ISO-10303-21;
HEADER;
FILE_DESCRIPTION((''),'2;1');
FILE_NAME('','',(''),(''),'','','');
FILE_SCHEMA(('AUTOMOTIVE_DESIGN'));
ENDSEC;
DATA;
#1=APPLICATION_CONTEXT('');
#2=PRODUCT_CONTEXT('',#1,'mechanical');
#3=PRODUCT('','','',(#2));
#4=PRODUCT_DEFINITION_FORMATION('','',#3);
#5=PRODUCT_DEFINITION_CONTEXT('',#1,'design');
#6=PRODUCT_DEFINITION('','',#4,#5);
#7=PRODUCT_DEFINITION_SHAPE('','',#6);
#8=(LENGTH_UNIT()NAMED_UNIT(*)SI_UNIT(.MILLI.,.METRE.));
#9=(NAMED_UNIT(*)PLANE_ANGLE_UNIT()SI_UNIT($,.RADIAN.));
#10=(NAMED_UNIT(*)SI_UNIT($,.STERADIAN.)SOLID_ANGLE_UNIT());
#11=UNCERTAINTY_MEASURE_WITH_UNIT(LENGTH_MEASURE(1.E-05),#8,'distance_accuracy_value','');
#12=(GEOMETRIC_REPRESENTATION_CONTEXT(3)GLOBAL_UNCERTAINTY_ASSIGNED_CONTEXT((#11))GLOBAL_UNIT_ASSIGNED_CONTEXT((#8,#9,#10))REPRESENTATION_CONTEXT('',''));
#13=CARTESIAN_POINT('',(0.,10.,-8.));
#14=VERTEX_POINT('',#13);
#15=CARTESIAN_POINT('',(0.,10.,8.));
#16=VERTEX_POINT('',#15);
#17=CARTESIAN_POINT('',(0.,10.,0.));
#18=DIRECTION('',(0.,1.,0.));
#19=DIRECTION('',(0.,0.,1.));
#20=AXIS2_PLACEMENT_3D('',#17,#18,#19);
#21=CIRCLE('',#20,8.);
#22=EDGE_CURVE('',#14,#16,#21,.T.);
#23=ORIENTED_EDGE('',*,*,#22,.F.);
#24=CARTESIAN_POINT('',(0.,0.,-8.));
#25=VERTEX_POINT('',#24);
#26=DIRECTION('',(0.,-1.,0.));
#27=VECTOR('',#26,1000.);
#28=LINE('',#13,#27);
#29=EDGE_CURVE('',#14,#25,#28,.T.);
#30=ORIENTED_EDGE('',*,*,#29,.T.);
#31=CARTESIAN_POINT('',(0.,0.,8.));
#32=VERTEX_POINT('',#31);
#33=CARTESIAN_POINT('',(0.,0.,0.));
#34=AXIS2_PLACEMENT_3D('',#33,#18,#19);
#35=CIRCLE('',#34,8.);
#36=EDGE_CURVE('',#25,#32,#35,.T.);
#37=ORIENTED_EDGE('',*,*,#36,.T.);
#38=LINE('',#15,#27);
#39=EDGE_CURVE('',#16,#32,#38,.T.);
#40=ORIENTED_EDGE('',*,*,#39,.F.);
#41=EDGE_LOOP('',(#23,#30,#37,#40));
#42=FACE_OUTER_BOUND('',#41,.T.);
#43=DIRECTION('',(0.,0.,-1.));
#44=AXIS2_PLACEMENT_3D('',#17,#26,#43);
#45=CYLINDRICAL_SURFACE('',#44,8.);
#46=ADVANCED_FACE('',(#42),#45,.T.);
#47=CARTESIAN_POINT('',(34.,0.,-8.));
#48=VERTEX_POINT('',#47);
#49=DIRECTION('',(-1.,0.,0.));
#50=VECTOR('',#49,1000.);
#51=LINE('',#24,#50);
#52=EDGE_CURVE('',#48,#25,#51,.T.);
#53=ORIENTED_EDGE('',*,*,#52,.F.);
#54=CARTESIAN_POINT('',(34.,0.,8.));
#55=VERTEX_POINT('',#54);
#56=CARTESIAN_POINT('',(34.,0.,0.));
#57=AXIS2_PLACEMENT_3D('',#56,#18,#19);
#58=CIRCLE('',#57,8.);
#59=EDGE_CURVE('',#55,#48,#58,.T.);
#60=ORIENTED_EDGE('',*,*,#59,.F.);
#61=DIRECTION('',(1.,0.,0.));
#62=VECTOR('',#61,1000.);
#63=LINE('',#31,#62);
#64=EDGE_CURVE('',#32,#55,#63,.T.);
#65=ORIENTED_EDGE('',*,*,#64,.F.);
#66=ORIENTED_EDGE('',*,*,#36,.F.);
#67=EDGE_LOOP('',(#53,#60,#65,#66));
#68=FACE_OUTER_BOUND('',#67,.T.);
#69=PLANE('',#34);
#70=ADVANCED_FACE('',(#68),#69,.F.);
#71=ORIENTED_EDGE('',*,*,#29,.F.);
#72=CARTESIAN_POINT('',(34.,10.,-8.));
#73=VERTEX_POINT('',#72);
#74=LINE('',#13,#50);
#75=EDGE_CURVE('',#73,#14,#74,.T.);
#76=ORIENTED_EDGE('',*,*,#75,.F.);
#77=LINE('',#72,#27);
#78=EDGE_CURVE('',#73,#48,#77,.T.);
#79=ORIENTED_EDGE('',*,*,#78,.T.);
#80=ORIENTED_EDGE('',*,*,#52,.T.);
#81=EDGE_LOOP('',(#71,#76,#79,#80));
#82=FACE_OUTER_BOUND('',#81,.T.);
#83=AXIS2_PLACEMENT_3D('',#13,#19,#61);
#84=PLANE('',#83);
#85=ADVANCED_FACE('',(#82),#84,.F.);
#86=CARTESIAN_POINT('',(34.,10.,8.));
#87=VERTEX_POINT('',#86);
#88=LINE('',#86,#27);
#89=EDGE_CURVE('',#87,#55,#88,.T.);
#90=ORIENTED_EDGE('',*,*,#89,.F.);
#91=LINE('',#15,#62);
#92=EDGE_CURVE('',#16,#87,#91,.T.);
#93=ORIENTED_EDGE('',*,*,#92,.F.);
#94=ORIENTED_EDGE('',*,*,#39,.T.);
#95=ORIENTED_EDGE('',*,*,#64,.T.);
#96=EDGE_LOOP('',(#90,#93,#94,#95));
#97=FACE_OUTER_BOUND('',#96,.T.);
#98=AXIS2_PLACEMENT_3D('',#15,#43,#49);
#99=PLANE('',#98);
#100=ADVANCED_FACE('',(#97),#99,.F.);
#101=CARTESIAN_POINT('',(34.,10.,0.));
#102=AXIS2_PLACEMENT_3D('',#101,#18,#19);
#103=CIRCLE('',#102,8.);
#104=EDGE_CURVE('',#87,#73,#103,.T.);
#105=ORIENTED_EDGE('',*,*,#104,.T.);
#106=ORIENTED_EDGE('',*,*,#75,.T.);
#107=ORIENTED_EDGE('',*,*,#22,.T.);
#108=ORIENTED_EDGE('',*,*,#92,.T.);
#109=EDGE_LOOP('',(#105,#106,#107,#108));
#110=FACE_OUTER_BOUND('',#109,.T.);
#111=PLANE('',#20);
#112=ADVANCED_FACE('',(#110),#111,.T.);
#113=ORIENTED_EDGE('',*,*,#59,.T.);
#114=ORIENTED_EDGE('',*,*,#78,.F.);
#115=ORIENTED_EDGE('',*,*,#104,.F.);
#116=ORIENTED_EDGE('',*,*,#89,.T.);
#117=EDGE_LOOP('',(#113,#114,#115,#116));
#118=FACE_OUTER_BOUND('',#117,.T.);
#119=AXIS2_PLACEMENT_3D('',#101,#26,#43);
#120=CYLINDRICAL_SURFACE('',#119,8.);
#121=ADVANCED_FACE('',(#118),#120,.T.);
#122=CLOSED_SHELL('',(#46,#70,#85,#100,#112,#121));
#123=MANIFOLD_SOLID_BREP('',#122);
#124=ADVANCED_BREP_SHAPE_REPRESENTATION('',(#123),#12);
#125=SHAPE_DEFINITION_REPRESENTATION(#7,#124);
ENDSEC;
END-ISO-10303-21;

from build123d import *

# Parameters (mm, degrees)
BOSS_EXTRUDE1_DEPTH = 10


with BuildPart() as part:
    # Sketch1 → Boss-Extrude1 (new body)
    with BuildSketch(Plane(origin=(0, 0, 0), x_dir=(1, 0, 0), z_dir=(0, 1, 0))):
        with BuildLine():
            Line((0, 8), (34, 8))
            ThreePointArc((34, 8), (42, 0), (34, -8))
            Line((34, -8), (0, -8))
            ThreePointArc((0, -8), (-8, 0), (0, 8))
        make_face()
    extrude(amount=BOSS_EXTRUDE1_DEPTH)


solid = part.part
